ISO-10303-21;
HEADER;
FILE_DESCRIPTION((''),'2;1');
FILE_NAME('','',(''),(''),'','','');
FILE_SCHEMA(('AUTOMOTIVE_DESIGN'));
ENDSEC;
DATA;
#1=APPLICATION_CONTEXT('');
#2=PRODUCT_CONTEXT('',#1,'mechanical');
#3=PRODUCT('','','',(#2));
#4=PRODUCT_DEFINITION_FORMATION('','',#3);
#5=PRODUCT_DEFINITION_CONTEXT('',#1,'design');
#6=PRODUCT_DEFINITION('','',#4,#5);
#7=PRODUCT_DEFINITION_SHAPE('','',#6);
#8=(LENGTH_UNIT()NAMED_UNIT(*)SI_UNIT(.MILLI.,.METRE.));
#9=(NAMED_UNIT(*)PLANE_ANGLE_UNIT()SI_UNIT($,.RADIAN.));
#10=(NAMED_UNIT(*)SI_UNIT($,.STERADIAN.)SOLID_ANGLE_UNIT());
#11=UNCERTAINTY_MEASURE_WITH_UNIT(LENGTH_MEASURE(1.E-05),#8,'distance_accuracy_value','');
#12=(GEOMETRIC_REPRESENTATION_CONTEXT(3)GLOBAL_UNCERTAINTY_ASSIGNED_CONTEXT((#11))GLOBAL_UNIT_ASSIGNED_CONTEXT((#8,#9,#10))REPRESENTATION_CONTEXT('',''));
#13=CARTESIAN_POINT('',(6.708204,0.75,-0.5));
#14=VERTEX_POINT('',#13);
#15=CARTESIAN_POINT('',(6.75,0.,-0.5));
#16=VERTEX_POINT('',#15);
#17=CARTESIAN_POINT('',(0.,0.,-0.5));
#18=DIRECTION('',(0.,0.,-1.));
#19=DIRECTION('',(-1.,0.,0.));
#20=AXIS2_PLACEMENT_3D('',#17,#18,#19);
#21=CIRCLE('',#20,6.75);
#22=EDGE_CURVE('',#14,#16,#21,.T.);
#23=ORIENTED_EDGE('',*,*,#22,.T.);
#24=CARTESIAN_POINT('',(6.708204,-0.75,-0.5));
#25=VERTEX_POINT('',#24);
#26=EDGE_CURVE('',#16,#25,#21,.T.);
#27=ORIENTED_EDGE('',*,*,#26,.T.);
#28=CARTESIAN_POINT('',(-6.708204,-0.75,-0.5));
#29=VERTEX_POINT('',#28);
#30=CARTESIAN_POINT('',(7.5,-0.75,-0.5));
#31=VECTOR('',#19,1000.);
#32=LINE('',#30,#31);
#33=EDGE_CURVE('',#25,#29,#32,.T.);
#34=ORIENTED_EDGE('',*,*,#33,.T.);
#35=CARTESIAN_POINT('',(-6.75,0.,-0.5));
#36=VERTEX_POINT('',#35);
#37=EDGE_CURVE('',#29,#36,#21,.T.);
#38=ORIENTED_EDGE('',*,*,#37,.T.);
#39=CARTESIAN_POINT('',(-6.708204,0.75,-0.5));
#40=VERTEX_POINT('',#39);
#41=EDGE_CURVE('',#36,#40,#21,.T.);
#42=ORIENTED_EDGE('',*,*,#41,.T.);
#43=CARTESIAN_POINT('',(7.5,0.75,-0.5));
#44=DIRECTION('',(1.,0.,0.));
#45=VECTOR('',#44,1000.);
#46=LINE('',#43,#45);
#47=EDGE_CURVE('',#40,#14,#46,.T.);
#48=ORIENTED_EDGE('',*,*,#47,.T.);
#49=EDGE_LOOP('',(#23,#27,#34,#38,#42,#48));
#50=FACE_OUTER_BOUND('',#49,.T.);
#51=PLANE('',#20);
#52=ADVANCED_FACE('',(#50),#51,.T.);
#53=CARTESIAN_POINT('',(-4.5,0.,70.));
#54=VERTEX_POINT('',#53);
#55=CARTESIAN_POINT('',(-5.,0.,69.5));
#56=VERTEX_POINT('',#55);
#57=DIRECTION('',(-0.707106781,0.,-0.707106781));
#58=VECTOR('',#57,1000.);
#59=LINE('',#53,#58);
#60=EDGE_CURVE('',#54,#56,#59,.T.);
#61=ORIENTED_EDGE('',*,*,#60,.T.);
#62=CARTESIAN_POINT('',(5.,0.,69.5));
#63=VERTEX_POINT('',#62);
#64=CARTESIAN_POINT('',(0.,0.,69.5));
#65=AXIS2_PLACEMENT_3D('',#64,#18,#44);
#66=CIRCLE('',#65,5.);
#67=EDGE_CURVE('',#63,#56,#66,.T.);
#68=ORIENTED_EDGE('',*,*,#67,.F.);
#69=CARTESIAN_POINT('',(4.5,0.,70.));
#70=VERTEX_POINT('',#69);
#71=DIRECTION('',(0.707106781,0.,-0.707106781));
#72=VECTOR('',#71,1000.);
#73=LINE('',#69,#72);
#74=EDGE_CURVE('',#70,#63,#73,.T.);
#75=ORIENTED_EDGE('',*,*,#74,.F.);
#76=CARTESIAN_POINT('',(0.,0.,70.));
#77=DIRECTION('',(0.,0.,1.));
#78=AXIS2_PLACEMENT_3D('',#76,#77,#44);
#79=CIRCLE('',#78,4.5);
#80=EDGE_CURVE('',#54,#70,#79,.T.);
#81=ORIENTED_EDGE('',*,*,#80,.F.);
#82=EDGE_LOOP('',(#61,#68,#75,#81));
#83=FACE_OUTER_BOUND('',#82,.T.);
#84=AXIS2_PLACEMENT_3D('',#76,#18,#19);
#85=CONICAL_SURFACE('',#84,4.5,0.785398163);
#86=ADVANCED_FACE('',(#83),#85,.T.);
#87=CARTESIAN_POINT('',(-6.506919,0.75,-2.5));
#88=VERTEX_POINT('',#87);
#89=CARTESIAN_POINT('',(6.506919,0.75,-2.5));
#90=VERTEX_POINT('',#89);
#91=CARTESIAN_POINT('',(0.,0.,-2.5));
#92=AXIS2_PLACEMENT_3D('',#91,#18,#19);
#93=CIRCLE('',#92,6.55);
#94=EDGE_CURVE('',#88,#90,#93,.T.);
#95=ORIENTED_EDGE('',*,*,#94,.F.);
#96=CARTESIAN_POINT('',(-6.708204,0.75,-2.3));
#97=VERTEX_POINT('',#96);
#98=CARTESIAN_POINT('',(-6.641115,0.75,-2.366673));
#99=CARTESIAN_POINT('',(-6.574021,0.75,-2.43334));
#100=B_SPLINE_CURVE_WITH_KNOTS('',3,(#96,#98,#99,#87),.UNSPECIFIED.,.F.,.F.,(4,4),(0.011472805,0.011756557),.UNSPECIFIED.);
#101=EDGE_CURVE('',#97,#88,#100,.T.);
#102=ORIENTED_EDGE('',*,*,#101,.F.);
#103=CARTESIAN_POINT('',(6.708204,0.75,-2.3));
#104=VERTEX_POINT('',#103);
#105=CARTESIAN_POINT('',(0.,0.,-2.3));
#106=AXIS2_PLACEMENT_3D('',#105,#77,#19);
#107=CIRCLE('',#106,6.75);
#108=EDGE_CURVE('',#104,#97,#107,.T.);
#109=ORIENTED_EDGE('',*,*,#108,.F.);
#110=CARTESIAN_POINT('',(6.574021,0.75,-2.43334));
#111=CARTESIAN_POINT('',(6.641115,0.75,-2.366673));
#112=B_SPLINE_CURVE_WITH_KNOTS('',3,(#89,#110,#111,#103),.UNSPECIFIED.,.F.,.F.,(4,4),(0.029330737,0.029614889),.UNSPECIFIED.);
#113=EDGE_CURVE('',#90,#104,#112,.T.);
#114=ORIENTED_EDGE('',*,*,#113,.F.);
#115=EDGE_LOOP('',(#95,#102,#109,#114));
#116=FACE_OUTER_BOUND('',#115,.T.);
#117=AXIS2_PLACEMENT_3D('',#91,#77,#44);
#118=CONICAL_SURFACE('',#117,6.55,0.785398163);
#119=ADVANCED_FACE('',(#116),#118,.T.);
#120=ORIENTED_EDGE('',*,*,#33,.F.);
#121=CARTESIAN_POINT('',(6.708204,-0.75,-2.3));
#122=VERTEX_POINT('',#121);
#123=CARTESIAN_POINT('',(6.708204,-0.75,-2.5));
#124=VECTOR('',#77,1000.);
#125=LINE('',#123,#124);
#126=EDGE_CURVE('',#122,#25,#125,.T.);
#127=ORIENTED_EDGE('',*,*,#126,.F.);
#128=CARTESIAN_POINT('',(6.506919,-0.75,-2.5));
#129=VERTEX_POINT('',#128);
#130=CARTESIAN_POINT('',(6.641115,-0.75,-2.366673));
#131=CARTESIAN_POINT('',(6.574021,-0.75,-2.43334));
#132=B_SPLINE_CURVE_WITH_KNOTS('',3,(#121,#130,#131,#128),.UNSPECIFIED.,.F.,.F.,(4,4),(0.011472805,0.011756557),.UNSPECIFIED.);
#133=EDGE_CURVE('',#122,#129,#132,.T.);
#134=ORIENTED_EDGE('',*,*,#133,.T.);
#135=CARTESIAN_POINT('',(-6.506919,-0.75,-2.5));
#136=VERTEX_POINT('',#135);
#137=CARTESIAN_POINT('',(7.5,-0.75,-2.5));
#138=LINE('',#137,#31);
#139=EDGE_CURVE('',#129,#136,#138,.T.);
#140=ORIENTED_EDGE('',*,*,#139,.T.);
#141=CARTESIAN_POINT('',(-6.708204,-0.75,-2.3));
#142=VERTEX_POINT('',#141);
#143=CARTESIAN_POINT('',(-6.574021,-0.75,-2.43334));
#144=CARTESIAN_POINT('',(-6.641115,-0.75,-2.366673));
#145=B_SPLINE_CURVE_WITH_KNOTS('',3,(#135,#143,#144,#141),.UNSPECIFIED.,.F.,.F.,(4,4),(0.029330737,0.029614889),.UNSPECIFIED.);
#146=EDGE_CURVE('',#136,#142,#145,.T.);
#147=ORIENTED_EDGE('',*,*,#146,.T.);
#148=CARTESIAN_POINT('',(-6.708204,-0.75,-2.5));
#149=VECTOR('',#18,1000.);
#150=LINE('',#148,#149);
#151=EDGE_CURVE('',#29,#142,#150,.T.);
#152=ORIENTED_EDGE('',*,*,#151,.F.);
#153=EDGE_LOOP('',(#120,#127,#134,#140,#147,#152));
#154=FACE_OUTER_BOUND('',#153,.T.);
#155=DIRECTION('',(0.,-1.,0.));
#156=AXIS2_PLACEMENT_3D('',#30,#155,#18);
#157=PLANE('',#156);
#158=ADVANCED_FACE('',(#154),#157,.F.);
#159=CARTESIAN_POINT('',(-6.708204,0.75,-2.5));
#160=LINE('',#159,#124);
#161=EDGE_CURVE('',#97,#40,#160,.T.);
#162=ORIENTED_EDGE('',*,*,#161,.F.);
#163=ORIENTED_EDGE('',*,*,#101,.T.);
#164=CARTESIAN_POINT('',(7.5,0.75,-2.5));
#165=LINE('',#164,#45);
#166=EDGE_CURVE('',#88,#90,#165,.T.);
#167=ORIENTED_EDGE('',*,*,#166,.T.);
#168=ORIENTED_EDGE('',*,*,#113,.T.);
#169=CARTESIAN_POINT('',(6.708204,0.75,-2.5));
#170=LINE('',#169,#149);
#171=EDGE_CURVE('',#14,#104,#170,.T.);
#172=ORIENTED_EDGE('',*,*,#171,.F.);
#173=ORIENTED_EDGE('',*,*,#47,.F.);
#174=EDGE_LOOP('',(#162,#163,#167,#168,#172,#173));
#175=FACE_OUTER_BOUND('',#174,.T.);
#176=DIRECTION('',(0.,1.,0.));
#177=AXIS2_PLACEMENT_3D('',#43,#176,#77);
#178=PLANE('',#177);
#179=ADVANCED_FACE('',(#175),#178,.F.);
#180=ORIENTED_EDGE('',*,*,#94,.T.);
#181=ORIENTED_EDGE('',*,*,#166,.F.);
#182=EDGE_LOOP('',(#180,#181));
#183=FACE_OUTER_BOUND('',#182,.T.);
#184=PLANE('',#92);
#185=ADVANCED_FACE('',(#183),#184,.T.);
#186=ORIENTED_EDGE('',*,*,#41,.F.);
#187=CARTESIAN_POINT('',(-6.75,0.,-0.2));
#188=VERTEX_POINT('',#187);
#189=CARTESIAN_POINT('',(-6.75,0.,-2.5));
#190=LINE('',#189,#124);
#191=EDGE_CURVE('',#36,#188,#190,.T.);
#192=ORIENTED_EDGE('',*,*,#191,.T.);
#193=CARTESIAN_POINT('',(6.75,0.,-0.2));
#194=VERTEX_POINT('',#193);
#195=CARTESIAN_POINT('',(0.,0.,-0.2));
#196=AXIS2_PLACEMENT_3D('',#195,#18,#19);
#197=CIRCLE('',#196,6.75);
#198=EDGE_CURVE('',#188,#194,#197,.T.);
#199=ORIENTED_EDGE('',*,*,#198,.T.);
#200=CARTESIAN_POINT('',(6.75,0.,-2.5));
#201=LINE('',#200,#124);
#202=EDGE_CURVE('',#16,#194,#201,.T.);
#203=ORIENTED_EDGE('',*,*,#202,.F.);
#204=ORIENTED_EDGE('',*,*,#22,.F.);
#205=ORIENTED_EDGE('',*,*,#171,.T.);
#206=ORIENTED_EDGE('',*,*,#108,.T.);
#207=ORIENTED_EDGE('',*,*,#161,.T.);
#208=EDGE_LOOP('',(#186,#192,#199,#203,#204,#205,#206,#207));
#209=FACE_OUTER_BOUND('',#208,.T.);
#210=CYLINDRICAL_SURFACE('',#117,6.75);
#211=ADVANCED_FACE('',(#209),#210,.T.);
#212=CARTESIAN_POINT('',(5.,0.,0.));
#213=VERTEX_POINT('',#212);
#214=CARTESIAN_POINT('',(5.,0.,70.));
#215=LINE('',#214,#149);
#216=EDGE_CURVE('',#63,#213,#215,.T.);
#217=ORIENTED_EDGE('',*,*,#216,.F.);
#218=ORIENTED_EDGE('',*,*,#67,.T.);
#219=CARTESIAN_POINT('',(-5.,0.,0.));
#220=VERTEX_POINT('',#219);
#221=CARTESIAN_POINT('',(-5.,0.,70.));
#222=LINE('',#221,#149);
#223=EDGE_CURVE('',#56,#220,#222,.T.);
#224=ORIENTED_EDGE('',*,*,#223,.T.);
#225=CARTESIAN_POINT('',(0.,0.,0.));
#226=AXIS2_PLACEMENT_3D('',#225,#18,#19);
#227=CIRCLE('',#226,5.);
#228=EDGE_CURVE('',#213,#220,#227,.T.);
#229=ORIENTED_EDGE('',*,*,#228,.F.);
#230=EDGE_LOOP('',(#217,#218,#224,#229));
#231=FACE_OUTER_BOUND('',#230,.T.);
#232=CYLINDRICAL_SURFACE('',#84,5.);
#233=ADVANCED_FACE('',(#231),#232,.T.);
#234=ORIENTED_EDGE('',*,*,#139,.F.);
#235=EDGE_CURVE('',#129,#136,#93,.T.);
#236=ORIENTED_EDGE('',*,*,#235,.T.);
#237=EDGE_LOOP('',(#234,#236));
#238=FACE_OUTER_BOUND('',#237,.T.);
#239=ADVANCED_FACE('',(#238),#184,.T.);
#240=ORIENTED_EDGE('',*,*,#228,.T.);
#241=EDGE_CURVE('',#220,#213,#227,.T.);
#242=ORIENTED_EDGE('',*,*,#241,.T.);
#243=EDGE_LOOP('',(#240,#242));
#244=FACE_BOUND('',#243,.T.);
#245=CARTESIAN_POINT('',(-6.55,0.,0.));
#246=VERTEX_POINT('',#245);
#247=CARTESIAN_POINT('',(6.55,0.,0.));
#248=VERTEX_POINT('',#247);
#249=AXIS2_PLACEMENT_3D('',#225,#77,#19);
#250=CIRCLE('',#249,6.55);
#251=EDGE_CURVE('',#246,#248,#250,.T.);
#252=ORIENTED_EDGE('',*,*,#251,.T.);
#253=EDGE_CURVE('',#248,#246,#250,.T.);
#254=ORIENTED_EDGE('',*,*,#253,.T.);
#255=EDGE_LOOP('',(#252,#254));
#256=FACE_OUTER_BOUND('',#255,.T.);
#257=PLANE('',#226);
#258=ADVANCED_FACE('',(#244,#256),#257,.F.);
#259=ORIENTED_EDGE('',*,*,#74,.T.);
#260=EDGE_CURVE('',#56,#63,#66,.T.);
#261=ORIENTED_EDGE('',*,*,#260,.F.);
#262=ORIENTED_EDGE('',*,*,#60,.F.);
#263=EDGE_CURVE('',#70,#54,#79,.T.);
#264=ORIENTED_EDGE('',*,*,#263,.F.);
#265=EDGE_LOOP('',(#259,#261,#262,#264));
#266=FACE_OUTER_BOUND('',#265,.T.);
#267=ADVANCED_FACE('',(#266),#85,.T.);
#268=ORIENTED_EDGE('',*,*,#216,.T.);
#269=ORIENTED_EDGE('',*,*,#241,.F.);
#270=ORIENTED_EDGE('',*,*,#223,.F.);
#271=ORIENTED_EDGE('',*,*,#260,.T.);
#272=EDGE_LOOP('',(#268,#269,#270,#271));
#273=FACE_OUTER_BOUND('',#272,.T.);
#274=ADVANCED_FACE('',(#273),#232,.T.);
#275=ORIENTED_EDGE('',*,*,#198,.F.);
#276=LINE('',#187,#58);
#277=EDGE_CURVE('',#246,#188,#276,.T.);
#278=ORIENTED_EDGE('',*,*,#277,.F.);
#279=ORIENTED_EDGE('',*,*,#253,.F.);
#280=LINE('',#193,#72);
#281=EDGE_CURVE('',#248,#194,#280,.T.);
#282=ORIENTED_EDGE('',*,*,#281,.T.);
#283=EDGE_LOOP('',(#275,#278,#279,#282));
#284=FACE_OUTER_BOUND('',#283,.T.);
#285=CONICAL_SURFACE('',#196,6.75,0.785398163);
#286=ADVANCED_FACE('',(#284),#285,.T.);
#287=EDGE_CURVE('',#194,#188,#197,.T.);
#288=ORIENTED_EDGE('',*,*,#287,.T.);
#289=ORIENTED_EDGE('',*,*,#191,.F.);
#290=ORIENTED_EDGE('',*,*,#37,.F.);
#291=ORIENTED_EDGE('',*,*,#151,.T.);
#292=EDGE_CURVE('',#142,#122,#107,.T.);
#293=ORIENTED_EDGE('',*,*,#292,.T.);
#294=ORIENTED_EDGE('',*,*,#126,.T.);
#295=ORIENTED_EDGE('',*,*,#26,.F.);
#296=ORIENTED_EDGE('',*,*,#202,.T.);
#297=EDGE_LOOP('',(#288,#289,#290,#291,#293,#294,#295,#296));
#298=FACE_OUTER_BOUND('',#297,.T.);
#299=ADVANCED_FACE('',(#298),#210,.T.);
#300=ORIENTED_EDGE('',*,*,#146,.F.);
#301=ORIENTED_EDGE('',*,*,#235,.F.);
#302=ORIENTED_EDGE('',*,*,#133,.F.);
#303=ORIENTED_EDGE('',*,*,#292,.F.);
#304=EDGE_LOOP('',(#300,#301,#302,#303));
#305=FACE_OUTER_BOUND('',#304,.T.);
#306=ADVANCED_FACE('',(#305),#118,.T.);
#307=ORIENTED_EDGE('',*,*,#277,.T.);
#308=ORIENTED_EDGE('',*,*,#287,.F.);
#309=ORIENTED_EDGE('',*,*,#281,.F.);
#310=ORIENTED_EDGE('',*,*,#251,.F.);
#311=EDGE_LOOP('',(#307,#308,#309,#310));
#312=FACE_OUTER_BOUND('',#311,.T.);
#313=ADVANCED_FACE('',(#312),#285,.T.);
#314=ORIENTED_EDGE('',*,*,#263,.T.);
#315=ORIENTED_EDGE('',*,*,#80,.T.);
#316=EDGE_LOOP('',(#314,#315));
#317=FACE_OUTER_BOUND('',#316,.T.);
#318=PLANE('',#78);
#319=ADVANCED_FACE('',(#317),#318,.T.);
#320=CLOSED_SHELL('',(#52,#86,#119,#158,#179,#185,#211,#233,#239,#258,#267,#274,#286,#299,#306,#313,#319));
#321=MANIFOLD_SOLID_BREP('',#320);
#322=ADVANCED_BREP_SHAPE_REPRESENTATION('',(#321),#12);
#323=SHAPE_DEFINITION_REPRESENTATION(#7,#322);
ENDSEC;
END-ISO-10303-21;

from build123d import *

# Parameters (mm, degrees)
SKETCH_4_R          = 5
EXTRUDE_3_DEPTH     = 70
SKETCH_5_R          = 6.75
EXTRUDE_4_DEPTH     = 2.5
CHAMFER_1_SIZE      = 0.5
CHAMFER_2_SIZE      = 0.2
SKETCH_6_W          = 15
SKETCH_6_H          = 1.5
CUT_EXTRUDE_1_DEPTH = 2


with BuildPart() as part:
    # 草图4 → 凸台-拉伸3 (new body)
    with BuildSketch(Plane.XY):
        Circle(SKETCH_4_R)
    extrude(amount=EXTRUDE_3_DEPTH)

    # 草图5 → 凸台-拉伸4 (add)
    with BuildSketch(Plane(origin=(0, 0, 0), x_dir=(-1, 0, 0), z_dir=(0, 0, -1))):
        Circle(SKETCH_5_R)
    extrude(amount=EXTRUDE_4_DEPTH)

    # 倒角1
    chamfer_1_edges = [part.edges().sort_by_distance(p)[0] for p in [
        (-5, 0, 70),
    ]]
    chamfer(chamfer_1_edges, length=CHAMFER_1_SIZE)

    # 倒角2
    chamfer_2_edges = [part.edges().sort_by_distance(p)[0] for p in [
        (6.75, 0, 0),
        (6.75, 0, -2.5),
    ]]
    chamfer(chamfer_2_edges, length=CHAMFER_2_SIZE)

    # 草图6 → 切除-拉伸1 (cut)
    with BuildSketch(Plane(origin=(0, 0, -2.5), x_dir=(-1, 0, 0), z_dir=(0, 0, -1))):
        Rectangle(SKETCH_6_W, SKETCH_6_H)
    extrude(amount=-CUT_EXTRUDE_1_DEPTH, mode=Mode.SUBTRACT)


solid = part.part
